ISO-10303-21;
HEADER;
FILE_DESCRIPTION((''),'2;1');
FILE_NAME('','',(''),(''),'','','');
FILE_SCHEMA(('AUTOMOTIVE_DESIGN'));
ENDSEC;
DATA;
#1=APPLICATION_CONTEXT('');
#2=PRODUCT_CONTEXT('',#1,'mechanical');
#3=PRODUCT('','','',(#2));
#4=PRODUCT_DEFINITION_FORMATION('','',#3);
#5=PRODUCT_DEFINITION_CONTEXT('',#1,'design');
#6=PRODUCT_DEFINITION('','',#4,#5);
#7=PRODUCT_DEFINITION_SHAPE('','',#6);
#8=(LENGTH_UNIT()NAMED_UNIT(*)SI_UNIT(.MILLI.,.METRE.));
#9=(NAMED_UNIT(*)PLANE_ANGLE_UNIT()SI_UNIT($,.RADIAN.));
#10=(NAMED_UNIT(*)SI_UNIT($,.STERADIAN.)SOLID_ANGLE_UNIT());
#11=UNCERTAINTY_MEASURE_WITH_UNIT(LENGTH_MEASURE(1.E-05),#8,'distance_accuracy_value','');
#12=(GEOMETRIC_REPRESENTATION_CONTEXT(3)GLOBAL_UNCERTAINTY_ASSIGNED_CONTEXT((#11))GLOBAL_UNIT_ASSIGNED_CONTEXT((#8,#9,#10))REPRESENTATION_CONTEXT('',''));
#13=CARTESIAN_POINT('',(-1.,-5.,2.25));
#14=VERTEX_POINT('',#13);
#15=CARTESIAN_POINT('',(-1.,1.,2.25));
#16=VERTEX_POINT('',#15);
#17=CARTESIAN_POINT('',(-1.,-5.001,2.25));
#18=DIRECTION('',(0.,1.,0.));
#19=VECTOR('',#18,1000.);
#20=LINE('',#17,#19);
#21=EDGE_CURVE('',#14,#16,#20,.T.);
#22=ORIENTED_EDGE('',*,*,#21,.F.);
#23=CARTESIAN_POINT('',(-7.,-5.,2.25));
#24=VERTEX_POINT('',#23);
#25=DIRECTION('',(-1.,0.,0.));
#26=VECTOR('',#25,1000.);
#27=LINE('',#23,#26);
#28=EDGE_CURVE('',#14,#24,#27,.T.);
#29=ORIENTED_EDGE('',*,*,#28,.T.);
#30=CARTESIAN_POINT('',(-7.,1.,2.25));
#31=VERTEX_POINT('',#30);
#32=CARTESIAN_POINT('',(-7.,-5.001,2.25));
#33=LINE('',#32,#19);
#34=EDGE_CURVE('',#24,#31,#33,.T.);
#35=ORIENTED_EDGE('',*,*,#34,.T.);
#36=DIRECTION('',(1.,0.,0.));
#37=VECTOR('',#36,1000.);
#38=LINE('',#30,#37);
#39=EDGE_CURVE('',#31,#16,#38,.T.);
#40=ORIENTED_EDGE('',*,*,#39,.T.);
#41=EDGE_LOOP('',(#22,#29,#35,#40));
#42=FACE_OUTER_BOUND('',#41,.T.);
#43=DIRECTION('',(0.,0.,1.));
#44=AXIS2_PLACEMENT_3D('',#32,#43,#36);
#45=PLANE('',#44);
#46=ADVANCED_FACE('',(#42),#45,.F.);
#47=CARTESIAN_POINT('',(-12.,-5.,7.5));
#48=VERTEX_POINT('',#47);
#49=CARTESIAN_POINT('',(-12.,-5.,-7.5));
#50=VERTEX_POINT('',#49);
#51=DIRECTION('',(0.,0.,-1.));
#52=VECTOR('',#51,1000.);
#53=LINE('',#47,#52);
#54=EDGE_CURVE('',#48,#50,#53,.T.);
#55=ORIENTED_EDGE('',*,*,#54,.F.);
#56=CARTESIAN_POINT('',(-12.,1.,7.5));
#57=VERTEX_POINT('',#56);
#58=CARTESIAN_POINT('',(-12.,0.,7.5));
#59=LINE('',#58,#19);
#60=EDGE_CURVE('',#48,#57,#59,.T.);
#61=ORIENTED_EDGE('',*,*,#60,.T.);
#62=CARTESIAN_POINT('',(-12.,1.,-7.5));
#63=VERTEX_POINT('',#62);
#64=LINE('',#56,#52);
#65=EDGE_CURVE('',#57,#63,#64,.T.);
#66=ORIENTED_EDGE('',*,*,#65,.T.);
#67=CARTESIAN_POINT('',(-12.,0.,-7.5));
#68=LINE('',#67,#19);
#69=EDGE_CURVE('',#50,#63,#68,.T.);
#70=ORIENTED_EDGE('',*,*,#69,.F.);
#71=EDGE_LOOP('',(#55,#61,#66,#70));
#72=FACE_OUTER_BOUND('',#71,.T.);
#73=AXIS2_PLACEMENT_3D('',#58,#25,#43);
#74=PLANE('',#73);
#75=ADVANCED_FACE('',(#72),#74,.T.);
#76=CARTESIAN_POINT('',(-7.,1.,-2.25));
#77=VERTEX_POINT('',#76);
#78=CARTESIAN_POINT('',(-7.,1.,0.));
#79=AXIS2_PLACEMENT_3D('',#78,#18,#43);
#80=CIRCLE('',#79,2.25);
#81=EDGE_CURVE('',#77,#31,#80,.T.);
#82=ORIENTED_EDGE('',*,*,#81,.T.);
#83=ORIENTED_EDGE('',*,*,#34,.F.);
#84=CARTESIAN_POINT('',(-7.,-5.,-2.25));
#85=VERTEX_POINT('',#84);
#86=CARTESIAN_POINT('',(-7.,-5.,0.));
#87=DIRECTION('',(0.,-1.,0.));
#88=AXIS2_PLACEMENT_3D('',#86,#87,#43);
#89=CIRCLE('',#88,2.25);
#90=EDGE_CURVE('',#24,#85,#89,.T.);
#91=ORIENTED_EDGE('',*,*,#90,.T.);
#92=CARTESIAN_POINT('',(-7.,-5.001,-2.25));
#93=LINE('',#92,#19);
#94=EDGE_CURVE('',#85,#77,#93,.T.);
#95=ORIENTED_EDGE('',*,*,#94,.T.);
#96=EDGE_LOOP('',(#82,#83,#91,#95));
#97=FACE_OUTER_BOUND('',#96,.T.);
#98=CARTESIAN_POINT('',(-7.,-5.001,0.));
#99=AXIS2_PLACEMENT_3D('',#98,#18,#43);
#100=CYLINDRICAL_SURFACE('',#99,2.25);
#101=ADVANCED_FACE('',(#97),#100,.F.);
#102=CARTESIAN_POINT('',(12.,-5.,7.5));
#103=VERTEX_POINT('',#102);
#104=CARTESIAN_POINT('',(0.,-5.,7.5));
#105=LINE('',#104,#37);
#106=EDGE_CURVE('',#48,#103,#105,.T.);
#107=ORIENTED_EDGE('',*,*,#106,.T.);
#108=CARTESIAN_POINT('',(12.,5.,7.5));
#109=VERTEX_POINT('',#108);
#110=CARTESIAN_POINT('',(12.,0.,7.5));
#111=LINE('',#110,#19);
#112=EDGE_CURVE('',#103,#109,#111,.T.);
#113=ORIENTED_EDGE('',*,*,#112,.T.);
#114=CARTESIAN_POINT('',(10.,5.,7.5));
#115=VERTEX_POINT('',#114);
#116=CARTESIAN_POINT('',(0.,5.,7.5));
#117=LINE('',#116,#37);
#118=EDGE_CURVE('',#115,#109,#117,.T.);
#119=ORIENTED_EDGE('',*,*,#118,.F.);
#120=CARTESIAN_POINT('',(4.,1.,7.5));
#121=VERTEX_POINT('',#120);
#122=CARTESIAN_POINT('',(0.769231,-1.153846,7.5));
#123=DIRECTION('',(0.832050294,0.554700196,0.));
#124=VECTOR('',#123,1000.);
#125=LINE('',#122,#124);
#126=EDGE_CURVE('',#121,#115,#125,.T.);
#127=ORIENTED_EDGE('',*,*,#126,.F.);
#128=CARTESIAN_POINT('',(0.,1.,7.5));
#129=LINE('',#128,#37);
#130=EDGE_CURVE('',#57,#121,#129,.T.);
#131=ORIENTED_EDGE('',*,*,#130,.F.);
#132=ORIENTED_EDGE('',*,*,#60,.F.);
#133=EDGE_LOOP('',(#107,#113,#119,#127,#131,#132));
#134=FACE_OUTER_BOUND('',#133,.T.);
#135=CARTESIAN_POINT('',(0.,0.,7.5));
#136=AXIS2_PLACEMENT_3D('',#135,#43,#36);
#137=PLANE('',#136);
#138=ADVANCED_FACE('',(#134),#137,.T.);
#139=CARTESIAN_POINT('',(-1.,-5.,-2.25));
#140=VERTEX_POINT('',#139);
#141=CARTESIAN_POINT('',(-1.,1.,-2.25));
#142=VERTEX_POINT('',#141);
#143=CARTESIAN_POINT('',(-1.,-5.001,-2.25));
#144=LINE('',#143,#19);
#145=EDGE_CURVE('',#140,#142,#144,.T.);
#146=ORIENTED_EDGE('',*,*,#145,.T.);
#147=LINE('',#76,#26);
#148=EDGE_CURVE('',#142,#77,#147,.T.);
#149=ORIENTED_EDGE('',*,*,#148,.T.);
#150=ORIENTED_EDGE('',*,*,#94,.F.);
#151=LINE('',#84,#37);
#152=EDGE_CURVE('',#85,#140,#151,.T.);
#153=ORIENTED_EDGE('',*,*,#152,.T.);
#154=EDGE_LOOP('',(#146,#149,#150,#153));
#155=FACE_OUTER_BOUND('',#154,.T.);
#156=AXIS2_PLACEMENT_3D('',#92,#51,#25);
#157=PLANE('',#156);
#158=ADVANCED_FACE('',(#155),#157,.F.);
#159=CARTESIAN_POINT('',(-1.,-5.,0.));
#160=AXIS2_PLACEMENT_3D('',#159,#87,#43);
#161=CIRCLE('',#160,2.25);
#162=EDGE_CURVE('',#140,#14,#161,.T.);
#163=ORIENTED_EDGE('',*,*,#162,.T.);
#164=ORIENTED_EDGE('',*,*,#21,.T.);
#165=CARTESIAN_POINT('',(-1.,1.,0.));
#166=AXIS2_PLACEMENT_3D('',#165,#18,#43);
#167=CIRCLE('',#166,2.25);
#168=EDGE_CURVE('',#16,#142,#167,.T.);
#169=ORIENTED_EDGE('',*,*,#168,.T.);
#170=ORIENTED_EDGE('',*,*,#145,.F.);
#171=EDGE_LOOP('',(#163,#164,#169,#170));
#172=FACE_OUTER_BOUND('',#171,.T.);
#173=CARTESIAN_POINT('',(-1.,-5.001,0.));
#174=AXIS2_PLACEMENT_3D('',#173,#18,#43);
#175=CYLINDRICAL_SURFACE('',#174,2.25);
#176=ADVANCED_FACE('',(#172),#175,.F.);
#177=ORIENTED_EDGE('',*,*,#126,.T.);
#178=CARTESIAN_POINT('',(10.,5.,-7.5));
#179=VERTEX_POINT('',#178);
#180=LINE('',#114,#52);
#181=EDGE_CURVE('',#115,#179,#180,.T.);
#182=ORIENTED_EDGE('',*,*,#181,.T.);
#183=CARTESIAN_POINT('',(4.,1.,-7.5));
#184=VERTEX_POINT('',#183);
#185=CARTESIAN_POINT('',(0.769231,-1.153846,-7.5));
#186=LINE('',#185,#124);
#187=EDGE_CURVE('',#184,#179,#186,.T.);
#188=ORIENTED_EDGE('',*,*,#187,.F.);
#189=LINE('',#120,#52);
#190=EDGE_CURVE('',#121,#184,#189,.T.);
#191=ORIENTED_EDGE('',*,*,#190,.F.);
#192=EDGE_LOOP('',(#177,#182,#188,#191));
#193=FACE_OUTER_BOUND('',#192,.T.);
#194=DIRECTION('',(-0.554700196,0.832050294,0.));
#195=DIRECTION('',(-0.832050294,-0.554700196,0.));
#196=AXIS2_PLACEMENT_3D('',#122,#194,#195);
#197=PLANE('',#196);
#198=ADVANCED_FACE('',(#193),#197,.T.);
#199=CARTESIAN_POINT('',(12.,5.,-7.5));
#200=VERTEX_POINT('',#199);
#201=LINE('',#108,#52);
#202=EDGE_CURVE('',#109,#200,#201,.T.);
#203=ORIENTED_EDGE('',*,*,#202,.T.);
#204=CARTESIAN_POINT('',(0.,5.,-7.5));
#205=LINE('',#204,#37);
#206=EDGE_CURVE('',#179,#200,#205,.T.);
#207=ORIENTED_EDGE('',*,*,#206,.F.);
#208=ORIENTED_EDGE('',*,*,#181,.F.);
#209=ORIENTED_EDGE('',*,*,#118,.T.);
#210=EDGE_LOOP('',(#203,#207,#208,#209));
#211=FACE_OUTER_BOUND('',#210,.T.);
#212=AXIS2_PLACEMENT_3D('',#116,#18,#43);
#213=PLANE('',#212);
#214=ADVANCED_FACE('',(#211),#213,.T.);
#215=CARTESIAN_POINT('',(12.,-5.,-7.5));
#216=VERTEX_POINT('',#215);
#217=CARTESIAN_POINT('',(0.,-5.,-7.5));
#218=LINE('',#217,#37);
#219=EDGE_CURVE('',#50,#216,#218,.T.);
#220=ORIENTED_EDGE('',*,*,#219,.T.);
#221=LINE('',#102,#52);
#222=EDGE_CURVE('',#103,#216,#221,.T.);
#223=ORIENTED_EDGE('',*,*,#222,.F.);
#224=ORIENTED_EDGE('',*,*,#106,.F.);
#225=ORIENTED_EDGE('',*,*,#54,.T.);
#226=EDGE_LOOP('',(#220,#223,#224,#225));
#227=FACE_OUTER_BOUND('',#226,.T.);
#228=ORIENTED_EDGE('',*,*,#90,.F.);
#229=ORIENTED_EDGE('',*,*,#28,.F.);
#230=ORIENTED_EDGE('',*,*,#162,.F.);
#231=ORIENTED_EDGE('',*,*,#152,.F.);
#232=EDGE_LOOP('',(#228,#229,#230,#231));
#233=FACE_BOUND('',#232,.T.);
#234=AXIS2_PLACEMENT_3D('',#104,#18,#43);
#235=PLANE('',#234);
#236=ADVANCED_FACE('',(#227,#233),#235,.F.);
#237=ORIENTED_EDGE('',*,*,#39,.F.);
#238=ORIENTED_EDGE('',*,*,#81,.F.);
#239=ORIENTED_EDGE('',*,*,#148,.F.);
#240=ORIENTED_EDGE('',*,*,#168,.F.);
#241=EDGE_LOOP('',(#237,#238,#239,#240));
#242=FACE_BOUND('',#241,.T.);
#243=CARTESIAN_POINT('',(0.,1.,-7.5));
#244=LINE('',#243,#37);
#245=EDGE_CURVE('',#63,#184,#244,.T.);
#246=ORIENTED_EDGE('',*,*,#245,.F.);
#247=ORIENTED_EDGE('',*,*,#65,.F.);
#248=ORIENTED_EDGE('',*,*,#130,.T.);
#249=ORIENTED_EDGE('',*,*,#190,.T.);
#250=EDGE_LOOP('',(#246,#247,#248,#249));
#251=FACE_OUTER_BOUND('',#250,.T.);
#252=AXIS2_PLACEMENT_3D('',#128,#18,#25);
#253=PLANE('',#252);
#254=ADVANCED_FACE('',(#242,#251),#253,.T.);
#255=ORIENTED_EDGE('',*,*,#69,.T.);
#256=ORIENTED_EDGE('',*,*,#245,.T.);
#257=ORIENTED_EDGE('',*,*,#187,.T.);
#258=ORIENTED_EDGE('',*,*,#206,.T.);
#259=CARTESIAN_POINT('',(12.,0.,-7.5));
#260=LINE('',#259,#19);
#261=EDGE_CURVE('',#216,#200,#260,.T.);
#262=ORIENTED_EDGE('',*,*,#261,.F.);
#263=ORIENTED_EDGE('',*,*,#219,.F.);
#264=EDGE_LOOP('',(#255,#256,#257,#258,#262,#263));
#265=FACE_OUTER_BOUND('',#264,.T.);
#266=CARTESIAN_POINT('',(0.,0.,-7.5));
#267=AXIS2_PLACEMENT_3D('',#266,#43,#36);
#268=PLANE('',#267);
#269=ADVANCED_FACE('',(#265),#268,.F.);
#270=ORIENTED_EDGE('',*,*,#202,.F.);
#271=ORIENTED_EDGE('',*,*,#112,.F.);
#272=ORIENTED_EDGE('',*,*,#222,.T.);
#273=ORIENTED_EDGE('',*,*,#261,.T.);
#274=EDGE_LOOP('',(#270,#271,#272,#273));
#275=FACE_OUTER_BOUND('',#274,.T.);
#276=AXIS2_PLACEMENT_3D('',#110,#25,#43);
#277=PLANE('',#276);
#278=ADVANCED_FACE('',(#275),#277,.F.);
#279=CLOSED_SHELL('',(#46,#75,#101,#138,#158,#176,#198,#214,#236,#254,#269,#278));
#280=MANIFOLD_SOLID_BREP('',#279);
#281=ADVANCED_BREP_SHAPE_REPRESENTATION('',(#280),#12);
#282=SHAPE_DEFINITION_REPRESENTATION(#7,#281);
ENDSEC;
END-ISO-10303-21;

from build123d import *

# Parameters (mm, degrees)
BOSS_EXTRUDE1_DEPTH = 7.5
CUT_EXTRUDE1_REACH  = 17.37


with BuildPart() as part:
    # Sketch1 → Boss-Extrude1 (new, symmetric)
    with BuildSketch(Plane.XY):
        Polygon((4, 1), (-12, 1), (-12, -5), (12, -5), (12, 5), (10, 5), align=None)
    extrude(amount=BOSS_EXTRUDE1_DEPTH, both=True)

    # Sketch2 → Cut-Extrude1 (cut, up to next)
    with BuildSketch(Plane(origin=(0, 1, 0), x_dir=(1, 0, 0), z_dir=(0, 1, 0)), mode=Mode.PRIVATE) as cut_extrude1_sk1:
        with BuildLine():
            Line((-7, 2.25), (-1, 2.25))
            ThreePointArc((-1, 2.25), (1.25, 0), (-1, -2.25))
            Line((-1, -2.25), (-7, -2.25))
            ThreePointArc((-7, -2.25), (-9.25, 0), (-7, 2.25))
        make_face()
    cut_extrude1_tool1 = extrude(cut_extrude1_sk1.sketch, amount=-CUT_EXTRUDE1_REACH, mode=Mode.PRIVATE) & part.part
    add(cut_extrude1_tool1.solids().sort_by_distance((-4, 1, 0))[0], mode=Mode.SUBTRACT)


solid = part.part
